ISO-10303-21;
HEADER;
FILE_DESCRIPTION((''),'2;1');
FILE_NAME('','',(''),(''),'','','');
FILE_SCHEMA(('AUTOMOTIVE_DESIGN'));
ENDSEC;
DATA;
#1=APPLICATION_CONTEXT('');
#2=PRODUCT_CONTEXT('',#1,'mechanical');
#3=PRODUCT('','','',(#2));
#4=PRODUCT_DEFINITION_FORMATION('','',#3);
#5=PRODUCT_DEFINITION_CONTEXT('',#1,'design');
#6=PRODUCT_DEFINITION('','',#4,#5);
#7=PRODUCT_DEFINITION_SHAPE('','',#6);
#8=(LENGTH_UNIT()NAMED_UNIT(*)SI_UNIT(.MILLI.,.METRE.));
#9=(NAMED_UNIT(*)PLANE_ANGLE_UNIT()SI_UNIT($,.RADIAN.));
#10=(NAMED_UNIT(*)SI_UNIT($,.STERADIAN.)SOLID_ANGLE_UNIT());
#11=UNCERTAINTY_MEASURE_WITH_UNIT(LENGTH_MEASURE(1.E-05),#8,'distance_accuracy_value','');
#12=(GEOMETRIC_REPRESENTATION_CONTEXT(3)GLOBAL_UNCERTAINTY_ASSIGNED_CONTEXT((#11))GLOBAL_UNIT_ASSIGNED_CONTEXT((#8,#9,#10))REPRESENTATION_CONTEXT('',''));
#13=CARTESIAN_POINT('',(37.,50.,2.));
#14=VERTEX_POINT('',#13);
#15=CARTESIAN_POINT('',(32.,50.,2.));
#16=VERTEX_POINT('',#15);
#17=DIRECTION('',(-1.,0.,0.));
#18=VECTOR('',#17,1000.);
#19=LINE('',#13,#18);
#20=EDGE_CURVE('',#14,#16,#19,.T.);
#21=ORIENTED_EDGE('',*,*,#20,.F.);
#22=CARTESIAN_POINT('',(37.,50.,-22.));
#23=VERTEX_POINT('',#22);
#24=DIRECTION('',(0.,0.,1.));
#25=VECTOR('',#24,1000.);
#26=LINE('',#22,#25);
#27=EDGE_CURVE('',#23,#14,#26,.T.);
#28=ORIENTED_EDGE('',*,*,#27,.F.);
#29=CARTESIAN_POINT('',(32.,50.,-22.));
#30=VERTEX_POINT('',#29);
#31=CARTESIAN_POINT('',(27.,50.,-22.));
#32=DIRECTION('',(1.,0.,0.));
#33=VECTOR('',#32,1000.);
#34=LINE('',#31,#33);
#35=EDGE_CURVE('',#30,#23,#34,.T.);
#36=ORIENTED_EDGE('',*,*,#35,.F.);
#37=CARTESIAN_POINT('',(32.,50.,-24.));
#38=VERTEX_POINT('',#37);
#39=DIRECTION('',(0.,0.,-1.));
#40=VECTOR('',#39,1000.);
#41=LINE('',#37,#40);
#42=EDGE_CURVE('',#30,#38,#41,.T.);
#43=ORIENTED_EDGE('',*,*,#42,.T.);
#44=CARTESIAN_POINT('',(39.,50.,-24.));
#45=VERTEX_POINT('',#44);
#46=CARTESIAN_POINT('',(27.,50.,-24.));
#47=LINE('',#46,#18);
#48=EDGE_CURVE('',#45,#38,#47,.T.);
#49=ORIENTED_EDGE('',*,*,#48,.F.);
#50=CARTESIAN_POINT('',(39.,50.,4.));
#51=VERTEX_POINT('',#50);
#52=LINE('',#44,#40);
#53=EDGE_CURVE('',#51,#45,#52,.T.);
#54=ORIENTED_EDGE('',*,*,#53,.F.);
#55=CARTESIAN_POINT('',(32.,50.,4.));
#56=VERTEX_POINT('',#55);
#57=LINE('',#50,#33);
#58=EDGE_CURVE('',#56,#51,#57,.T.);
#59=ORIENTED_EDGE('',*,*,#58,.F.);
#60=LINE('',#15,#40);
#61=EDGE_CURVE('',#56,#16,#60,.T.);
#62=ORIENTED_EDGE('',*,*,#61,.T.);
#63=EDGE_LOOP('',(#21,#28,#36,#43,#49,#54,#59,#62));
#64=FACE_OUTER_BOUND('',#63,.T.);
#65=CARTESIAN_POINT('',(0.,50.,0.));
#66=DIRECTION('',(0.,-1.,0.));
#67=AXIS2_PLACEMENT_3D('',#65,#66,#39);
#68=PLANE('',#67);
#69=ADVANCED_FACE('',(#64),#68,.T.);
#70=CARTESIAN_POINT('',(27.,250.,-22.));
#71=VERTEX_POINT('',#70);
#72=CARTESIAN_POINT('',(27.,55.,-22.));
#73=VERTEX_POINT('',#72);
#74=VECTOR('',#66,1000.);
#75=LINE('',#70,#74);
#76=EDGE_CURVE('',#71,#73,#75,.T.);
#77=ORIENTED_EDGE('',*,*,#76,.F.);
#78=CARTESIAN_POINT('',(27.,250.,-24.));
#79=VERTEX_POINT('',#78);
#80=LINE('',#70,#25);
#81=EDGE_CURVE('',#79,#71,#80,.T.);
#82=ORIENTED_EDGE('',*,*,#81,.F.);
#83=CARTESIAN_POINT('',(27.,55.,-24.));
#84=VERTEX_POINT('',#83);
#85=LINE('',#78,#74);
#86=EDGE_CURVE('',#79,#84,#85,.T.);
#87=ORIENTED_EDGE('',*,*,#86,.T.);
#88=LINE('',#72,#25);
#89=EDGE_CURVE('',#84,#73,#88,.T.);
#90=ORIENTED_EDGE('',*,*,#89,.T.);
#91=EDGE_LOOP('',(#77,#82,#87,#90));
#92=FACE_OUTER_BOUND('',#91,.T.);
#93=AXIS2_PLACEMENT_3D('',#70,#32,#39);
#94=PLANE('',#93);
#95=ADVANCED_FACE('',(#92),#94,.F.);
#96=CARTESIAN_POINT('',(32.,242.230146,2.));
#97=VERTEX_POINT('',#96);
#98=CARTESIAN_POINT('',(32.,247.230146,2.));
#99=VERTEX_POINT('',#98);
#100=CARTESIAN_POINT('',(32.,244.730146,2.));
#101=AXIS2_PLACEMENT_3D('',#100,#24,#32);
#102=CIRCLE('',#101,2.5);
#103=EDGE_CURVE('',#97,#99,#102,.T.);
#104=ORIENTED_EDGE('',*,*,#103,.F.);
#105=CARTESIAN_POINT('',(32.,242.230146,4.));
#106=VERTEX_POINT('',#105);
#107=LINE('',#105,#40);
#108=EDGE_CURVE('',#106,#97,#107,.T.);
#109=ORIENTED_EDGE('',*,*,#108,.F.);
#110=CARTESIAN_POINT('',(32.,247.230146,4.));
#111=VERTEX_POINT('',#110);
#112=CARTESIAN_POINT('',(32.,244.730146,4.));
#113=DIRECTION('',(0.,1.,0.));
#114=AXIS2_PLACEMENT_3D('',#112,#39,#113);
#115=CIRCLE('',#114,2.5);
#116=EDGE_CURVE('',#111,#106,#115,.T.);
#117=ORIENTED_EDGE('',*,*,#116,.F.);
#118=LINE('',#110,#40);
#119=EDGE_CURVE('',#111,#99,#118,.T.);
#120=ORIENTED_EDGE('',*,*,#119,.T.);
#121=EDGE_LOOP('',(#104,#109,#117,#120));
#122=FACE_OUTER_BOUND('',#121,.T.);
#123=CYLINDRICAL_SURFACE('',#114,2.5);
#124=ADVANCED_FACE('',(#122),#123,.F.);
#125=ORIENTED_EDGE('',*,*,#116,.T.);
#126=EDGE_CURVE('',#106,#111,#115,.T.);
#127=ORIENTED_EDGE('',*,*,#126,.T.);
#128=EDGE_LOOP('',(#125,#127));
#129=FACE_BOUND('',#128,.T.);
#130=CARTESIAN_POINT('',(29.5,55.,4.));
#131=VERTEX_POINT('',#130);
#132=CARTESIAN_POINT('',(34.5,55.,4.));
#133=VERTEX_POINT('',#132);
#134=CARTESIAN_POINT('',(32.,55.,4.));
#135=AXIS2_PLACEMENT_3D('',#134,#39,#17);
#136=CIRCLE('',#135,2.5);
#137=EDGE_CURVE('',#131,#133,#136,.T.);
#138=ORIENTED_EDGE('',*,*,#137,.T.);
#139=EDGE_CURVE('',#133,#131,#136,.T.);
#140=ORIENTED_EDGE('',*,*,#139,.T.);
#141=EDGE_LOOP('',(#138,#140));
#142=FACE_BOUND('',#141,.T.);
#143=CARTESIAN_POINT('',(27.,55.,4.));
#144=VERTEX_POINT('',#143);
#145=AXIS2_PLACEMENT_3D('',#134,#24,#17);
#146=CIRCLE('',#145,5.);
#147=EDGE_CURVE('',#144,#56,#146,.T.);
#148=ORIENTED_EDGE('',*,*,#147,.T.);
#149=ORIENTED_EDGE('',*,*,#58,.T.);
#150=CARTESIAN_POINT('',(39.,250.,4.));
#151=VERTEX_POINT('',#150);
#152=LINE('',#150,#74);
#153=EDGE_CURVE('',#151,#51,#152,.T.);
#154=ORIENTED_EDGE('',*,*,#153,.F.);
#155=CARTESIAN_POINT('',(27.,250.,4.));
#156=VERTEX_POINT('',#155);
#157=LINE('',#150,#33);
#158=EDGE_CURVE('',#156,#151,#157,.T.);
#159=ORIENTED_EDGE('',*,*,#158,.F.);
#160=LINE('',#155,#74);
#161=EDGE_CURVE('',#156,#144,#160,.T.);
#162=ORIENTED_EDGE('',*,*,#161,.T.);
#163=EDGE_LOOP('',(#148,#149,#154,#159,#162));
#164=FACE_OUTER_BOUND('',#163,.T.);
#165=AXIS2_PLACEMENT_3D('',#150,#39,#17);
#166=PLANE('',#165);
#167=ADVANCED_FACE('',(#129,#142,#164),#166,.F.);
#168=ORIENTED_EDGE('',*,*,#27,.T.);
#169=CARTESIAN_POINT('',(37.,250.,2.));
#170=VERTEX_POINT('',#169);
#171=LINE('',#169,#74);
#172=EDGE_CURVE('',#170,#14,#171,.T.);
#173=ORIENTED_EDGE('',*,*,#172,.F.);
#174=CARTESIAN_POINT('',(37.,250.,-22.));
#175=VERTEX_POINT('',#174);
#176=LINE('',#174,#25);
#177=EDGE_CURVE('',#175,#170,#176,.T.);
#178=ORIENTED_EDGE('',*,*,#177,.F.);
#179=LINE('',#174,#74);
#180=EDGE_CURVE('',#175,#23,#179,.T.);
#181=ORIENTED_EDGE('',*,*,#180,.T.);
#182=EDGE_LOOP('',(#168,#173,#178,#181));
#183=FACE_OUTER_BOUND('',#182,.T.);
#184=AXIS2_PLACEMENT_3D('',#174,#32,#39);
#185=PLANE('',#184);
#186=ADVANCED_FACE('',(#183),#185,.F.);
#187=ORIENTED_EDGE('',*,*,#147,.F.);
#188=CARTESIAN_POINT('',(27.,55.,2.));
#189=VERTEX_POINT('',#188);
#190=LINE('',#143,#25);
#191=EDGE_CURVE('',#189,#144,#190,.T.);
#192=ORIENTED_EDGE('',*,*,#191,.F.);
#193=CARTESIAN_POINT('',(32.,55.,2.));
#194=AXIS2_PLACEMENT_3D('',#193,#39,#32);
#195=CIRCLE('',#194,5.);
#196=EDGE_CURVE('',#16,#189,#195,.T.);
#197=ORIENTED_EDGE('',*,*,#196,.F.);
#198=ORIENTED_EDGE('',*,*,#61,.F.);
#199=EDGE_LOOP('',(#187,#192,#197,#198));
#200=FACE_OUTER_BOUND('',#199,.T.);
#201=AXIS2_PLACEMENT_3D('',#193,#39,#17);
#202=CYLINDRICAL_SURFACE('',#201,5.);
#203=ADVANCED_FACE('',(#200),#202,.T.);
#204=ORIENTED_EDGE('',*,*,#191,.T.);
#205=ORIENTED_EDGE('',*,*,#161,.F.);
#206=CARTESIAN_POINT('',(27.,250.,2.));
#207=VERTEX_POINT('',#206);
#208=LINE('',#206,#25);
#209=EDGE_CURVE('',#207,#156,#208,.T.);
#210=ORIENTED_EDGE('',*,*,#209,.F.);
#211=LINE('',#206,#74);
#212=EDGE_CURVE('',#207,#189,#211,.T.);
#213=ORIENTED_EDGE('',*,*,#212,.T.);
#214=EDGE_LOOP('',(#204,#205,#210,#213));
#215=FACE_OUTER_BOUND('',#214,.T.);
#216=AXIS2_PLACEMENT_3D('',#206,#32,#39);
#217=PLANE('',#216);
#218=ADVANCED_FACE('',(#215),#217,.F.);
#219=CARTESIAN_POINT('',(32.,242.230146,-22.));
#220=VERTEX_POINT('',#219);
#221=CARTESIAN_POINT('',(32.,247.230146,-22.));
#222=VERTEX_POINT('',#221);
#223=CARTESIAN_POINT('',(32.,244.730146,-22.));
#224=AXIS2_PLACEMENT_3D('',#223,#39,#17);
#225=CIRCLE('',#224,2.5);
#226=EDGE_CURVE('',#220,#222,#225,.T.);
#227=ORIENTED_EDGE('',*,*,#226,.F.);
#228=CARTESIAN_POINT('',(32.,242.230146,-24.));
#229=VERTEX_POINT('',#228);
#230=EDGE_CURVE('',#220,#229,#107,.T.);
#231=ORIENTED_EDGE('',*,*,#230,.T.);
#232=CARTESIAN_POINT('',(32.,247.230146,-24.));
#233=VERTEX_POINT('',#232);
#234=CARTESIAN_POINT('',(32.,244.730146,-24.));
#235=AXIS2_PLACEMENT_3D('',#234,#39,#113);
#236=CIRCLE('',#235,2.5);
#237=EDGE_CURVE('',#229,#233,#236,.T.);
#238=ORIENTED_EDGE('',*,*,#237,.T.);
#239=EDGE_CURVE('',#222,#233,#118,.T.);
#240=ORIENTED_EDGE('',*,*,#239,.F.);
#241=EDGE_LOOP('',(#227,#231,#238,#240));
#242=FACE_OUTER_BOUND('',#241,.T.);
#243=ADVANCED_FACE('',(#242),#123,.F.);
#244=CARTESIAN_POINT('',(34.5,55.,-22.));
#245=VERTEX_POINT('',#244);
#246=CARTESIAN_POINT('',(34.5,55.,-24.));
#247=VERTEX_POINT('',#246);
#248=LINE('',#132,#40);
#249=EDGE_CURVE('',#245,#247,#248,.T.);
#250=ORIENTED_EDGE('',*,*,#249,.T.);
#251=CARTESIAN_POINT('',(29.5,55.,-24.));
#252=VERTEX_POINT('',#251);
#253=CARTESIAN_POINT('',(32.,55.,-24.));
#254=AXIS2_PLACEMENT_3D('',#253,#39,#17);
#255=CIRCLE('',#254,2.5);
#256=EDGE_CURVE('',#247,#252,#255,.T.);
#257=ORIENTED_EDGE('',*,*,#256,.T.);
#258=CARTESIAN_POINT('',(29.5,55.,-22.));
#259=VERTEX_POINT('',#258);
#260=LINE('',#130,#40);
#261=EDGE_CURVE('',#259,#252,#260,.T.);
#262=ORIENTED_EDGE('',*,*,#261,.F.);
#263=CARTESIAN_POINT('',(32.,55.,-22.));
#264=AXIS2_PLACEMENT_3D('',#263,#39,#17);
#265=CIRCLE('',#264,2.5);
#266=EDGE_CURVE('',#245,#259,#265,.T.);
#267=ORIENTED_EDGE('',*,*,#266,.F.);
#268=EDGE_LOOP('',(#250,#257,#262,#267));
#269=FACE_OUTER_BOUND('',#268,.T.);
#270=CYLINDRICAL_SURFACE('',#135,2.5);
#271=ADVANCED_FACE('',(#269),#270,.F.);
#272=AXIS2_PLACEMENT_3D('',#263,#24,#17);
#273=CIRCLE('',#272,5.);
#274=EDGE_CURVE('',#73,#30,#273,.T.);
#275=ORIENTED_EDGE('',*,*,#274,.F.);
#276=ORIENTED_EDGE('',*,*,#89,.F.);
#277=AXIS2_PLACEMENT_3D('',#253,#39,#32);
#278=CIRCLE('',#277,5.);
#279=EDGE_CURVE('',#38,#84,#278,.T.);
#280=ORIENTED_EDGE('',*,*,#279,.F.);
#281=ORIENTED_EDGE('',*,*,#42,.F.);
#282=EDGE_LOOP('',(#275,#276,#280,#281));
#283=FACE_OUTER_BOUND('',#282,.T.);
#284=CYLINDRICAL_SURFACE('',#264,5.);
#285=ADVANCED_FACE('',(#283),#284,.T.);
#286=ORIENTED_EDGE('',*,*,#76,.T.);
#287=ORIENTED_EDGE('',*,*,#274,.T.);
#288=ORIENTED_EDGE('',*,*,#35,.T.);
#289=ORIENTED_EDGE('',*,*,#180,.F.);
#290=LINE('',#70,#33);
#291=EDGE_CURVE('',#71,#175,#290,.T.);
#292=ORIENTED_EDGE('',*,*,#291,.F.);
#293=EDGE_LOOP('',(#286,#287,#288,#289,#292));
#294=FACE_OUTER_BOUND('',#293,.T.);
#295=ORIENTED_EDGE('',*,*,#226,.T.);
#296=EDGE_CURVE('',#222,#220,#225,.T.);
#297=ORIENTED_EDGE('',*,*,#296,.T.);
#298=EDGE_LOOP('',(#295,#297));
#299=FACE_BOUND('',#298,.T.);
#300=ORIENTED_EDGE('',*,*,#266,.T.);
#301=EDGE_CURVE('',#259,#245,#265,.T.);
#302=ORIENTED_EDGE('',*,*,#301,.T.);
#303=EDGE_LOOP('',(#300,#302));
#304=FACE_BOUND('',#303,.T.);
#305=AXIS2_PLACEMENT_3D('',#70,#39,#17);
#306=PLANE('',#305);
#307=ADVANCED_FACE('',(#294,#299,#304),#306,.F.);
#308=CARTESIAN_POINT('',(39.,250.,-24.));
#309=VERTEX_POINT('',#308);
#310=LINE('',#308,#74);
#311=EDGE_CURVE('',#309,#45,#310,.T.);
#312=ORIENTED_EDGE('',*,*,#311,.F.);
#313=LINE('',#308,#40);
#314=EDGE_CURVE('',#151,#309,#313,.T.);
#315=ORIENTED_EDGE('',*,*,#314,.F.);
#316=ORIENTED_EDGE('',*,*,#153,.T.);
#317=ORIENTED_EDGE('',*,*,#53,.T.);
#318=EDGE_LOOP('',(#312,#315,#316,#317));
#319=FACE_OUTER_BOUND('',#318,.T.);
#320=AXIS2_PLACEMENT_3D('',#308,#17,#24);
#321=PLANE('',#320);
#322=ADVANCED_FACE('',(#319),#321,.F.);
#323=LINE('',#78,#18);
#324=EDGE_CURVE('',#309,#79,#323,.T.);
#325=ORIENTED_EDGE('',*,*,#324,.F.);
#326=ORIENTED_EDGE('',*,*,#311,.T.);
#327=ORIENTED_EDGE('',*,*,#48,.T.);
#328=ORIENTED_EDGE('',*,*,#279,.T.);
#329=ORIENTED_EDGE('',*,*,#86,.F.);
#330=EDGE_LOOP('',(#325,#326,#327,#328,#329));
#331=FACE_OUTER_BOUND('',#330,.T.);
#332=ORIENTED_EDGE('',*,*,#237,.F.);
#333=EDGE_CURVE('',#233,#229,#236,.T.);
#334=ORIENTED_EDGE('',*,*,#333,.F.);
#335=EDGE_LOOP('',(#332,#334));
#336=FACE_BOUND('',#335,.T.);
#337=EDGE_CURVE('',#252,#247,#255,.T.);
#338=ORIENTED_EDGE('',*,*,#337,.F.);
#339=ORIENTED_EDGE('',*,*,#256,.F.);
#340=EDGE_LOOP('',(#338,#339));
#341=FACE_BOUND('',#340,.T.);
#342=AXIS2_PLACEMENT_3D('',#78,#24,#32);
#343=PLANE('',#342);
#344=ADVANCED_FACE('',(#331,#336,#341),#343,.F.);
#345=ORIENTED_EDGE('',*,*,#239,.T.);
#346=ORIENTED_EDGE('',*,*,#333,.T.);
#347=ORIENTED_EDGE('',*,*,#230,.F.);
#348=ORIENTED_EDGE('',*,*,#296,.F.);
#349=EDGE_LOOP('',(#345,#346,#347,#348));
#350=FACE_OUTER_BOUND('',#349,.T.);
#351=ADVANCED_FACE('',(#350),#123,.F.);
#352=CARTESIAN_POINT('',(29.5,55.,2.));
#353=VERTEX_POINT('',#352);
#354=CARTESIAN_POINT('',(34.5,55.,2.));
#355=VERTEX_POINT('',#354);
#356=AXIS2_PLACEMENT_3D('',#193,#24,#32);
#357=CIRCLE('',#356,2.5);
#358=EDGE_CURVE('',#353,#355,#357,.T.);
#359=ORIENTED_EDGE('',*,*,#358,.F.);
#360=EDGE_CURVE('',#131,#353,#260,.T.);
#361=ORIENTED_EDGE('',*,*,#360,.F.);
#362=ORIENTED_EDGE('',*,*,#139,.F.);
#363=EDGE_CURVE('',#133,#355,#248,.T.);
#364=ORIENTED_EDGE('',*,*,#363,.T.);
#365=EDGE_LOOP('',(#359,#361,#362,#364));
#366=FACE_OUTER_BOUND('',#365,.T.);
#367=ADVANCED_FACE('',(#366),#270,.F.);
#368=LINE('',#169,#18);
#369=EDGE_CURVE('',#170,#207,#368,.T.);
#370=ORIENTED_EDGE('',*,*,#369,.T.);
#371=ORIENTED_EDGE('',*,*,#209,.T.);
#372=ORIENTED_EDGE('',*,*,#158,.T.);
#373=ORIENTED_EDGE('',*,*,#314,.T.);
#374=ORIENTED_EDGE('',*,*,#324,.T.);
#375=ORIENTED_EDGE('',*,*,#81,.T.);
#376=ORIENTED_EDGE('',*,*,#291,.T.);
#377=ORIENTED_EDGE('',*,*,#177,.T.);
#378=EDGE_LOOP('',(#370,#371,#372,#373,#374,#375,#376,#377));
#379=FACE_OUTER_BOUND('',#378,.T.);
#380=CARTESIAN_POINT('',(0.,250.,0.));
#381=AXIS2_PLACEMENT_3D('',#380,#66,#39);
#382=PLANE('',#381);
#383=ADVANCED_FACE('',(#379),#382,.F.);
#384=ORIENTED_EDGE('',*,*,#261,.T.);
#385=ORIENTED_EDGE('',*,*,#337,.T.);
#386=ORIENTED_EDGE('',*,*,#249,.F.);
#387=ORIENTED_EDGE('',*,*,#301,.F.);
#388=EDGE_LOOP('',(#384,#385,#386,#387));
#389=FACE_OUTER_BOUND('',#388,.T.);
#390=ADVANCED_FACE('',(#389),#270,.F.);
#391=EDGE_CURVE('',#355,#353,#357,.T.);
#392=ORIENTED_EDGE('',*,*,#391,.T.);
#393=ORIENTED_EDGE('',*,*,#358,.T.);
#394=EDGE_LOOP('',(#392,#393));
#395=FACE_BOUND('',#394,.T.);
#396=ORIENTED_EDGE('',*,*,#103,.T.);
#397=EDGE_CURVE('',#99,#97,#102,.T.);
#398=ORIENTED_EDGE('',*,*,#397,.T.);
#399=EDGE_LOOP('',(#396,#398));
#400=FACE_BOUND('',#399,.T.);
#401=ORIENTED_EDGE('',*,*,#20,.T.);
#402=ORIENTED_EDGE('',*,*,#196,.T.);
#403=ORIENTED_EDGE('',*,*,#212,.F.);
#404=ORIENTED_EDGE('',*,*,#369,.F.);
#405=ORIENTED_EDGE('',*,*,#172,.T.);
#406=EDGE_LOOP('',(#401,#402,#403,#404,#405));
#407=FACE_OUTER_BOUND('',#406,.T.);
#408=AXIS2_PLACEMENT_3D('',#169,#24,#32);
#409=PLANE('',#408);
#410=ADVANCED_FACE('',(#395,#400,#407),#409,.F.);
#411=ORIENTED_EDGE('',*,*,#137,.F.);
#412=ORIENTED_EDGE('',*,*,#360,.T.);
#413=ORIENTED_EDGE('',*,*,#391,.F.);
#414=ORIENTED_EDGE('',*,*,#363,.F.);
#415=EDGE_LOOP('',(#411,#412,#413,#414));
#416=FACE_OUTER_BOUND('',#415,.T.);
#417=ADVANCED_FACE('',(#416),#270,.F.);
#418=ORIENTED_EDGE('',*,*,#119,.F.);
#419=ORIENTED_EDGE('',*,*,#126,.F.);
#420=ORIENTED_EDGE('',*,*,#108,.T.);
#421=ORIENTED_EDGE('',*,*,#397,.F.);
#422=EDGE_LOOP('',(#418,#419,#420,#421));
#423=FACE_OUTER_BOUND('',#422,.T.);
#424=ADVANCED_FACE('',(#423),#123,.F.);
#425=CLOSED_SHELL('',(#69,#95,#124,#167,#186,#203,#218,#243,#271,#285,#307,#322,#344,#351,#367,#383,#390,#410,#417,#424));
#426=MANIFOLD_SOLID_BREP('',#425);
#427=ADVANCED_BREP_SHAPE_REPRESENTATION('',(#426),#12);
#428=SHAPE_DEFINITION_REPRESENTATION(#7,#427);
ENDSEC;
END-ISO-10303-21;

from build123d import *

# Parameters (mm, degrees)
BOSS_EXTRUDE1_DEPTH     = 200
FILLET1_R               = 5
CUT_EXTRUDE1_DEPTH      = 255.356049663
CUT_EXTRUDE1_DEPTH_BACK = 255.356049663
SKETCH3_R               = 2.5
CUT_EXTRUDE2_DEPTH      = 255.356049663
CUT_EXTRUDE2_DEPTH_BACK = 255.356049663
SKETCH9_R               = 2.5


with BuildPart() as part:
    # Sketch2 → Boss-Extrude1 (new body)
    with BuildSketch(Plane(origin=(0, 50, 0), x_dir=(1, 0, 0), z_dir=(0, 1, 0))):
        Polygon((27, 22), (37, 22), (37, -2), (27, -2), (27, -4), (39, -4), (39, 24), (27, 24), align=None)
    extrude(amount=BOSS_EXTRUDE1_DEPTH)

    # Fillet1
    fillet1_edges = [part.edges().sort_by_distance(p)[0] for p in [
        (27, 50, 3),
        (27, 50, -23),
    ]]
    fillet(fillet1_edges, radius=FILLET1_R)

    # Sketch3 → Cut-Extrude1 (cut, two sides: drawn at the far end of the back side and taken through both)
    with BuildSketch(Plane(origin=(0, 0, 2), x_dir=(-1, 0, 0), z_dir=(0, 0, -1)).offset(-CUT_EXTRUDE1_DEPTH_BACK)):
        with Locations((-32, 55)):
            Circle(SKETCH3_R)
    extrude(amount=CUT_EXTRUDE1_DEPTH + CUT_EXTRUDE1_DEPTH_BACK, mode=Mode.SUBTRACT)

    # Sketch9 → Cut-Extrude2 (cut, two sides: drawn at the far end of the back side and taken through both)
    with BuildSketch(Plane(origin=(0, 0, -22), x_dir=(-1, 0, 0), z_dir=(0, 0, -1)).offset(-CUT_EXTRUDE2_DEPTH_BACK)):
        with Locations(Location((-32, 244.730145932, 0), (0, 0, 90))):
            Circle(SKETCH9_R)
    extrude(amount=CUT_EXTRUDE2_DEPTH + CUT_EXTRUDE2_DEPTH_BACK, mode=Mode.SUBTRACT)


solid = part.part
